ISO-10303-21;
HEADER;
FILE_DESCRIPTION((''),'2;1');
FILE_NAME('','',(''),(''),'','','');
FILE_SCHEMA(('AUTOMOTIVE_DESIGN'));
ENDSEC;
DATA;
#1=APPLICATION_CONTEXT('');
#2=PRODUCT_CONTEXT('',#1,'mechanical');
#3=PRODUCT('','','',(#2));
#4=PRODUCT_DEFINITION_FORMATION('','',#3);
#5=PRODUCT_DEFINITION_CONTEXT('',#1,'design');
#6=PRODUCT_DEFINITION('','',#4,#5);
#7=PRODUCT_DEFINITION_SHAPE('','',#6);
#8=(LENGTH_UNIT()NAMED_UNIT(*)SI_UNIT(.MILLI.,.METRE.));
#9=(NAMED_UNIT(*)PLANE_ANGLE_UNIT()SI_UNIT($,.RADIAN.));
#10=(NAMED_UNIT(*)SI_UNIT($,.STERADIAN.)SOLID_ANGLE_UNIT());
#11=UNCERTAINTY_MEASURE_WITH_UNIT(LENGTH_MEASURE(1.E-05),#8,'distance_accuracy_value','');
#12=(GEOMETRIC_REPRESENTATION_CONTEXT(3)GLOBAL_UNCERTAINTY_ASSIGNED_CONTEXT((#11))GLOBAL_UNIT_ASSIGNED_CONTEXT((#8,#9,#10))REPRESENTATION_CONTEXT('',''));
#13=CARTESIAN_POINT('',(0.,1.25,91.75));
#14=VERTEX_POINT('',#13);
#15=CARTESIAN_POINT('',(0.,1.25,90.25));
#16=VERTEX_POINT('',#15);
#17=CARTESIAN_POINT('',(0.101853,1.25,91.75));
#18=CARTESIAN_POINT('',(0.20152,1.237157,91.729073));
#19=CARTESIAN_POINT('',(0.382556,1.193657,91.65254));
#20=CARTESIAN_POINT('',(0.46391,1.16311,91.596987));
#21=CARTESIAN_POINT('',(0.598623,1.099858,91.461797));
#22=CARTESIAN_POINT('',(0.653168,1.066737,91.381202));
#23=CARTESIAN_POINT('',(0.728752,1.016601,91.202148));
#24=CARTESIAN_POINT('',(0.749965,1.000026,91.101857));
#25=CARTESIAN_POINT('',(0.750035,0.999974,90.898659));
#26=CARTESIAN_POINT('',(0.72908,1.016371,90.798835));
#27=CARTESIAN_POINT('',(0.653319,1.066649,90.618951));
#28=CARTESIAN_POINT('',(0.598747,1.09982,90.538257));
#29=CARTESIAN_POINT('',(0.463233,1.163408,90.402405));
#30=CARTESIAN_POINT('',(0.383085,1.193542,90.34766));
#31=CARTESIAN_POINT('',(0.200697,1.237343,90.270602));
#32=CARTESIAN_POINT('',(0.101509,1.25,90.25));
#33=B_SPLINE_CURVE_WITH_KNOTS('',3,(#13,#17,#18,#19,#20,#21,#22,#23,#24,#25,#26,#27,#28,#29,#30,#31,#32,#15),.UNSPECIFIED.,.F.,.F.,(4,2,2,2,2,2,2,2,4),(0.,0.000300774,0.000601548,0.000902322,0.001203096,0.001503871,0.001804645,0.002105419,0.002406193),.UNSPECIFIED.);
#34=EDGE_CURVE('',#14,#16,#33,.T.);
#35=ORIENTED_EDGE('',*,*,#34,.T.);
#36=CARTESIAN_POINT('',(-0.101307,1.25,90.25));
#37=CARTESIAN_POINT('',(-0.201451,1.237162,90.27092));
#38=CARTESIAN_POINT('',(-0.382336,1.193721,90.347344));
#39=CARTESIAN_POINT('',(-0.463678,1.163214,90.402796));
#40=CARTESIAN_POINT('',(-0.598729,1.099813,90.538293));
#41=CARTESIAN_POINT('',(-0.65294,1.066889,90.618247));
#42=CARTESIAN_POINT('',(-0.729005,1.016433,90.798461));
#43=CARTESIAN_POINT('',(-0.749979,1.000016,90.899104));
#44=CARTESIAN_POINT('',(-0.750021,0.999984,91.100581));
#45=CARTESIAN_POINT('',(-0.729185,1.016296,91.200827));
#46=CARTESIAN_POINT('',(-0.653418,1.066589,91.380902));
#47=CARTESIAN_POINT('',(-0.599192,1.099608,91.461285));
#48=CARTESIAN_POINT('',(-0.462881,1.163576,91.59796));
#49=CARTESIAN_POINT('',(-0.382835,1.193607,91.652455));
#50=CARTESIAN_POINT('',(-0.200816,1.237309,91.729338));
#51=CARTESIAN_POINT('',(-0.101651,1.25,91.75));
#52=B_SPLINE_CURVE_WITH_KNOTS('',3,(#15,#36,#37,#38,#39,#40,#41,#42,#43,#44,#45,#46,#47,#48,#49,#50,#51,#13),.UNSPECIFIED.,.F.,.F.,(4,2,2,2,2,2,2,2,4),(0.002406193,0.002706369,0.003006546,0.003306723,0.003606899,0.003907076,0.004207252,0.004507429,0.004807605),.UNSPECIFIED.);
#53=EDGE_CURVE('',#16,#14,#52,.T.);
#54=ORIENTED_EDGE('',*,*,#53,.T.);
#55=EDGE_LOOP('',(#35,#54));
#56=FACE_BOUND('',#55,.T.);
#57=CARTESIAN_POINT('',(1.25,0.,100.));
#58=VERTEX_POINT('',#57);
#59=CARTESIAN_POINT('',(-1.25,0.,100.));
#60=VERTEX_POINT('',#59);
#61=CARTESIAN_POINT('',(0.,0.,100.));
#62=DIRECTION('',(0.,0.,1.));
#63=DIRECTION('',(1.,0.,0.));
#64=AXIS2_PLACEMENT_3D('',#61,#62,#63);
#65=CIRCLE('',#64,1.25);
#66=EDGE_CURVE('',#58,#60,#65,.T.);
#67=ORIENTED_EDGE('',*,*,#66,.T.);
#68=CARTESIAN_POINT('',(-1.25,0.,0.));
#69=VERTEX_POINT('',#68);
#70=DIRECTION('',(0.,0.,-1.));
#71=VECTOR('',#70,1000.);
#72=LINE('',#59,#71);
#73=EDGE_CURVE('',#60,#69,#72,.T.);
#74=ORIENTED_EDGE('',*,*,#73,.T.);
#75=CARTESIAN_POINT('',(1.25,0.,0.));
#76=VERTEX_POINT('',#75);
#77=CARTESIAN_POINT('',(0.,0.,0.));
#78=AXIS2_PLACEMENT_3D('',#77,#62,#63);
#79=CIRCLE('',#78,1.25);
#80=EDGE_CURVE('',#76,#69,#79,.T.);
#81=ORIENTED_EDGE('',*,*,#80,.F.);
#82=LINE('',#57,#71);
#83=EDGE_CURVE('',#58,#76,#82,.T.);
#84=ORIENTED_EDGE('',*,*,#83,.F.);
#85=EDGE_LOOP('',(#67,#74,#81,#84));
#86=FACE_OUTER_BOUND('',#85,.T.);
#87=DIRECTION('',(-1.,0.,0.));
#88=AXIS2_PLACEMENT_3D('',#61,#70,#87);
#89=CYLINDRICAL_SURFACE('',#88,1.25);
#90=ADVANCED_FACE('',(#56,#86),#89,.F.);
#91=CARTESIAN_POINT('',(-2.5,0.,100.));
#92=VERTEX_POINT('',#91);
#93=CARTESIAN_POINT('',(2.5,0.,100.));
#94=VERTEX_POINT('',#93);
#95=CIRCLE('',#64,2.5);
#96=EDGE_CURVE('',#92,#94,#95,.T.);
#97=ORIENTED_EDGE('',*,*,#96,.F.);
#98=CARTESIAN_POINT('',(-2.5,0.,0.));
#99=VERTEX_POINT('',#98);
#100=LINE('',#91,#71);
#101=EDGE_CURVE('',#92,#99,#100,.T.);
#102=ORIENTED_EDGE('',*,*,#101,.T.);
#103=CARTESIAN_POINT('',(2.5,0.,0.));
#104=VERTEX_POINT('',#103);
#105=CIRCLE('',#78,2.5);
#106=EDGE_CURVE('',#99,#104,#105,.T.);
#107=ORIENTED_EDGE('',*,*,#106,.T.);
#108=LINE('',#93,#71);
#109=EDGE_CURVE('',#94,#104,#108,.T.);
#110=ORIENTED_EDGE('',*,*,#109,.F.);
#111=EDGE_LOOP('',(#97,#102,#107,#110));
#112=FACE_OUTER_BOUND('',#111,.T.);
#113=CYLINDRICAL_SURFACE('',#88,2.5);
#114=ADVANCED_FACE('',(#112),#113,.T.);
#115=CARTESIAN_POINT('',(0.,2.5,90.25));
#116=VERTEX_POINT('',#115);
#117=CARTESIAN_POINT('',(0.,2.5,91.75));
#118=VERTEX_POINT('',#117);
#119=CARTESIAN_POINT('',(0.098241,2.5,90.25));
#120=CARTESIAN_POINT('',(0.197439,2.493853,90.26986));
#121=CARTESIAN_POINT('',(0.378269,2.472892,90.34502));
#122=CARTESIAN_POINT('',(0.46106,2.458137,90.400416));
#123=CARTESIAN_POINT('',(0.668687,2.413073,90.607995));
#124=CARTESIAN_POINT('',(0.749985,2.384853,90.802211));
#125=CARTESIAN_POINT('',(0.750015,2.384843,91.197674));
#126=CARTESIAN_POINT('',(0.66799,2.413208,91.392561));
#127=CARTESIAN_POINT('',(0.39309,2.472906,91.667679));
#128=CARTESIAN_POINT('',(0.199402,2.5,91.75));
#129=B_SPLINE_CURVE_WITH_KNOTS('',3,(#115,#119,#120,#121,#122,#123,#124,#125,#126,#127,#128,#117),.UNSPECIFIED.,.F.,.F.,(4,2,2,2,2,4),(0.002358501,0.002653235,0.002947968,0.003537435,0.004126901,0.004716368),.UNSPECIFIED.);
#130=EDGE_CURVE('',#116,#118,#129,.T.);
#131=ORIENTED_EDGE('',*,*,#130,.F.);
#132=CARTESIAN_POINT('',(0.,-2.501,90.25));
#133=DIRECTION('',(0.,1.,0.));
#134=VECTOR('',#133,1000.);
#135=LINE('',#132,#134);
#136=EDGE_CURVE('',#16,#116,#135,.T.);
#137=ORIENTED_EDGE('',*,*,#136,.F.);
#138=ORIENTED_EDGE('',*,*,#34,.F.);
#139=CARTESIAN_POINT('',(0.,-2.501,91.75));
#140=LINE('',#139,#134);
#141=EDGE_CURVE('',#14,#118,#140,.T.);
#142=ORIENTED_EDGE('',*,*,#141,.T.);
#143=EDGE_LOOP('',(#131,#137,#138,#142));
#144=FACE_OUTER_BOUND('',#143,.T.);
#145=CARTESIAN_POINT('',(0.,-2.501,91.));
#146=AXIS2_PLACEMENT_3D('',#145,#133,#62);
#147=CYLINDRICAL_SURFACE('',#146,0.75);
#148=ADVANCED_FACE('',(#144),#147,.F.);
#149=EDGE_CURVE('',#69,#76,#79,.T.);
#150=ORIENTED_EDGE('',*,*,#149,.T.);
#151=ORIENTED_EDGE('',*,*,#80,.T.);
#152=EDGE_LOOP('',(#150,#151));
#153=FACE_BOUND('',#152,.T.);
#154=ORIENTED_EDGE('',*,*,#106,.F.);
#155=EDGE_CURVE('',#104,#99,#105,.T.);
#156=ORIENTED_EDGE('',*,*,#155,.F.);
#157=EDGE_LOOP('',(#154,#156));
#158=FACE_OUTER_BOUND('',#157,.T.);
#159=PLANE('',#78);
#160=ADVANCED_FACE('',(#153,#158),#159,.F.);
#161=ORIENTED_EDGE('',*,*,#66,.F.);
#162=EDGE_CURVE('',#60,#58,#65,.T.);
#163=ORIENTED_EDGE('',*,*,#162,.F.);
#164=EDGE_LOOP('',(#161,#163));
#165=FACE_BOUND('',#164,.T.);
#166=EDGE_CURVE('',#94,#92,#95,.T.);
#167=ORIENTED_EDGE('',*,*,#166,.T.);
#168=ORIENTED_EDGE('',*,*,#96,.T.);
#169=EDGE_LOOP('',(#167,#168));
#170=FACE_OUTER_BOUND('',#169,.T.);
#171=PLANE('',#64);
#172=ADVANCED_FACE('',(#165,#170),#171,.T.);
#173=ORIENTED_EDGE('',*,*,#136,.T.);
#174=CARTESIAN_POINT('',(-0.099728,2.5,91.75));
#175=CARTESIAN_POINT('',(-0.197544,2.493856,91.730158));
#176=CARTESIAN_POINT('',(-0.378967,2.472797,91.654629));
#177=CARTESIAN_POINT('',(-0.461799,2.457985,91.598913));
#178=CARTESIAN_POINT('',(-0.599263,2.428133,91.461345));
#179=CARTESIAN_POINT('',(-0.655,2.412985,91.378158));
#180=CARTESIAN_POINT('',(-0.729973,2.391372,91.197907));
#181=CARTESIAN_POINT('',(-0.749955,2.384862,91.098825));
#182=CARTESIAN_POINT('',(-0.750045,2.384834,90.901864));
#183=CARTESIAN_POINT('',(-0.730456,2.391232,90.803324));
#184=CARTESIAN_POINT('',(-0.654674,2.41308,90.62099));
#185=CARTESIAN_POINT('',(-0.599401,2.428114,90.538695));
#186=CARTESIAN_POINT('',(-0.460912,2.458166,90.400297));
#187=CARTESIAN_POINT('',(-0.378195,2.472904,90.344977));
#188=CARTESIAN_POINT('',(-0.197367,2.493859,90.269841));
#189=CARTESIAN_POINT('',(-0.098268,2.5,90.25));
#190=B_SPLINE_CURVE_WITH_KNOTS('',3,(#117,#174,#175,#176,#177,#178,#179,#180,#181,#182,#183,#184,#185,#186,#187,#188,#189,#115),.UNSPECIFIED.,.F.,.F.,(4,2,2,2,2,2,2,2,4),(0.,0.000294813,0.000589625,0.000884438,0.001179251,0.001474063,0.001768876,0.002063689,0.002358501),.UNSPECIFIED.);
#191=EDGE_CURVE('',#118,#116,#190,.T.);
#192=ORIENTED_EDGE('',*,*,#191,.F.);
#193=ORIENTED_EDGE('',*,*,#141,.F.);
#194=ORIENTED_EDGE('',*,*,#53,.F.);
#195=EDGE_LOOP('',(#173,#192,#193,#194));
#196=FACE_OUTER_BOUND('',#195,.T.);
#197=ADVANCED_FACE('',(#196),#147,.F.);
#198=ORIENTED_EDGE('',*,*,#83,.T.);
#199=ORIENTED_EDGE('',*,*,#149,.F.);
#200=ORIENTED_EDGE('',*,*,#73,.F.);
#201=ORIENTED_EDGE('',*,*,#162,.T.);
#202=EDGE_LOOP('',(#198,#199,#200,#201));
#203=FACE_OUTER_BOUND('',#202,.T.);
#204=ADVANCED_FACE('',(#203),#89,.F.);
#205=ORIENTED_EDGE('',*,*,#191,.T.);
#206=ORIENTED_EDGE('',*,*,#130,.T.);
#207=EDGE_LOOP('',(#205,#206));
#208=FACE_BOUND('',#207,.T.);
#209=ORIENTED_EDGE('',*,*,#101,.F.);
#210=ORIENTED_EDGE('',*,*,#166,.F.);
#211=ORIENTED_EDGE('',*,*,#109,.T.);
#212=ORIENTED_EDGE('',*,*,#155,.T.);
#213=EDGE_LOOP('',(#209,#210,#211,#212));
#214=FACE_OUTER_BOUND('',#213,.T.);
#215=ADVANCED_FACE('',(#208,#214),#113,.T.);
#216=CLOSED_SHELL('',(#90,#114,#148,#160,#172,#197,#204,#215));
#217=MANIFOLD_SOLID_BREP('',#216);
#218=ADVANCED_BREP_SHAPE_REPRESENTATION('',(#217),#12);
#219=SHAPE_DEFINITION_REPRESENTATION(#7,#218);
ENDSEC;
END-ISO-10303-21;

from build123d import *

# Parameters (mm, degrees)
SKETCH2_R               = 2.5
SKETCH2_R_2             = 1.25
BOSS_EXTRUDE1_DEPTH     = 100
CUT_EXTRUDE1_REACH      = 102.156
CUT_EXTRUDE1_END_RADIUS = 1.25
SKETCH3_R               = 0.75


with BuildPart() as part:
    # Sketch2 → Boss-Extrude1 (new body)
    with BuildSketch(Plane.XY):
        Circle(SKETCH2_R)
        Circle(SKETCH2_R_2, mode=Mode.SUBTRACT)
    extrude(amount=BOSS_EXTRUDE1_DEPTH)

    # Cut-Extrude1: up to this cylinder (the profile starts outside it)
    cut_extrude1_end = Plane(origin=(0, 0, 91), z_dir=(0, 0, -1)) * Cylinder(CUT_EXTRUDE1_END_RADIUS, 207.812, mode=Mode.PRIVATE)
    # Sketch3 → Cut-Extrude1 (cut, up to the surface)
    with BuildSketch(Plane(origin=(0, 2.5, 0), x_dir=(1, 0, 0), z_dir=(0, 1, 0)), mode=Mode.PRIVATE) as cut_extrude1_sk1:
        with Locations(Location((0, -91, 0), (0, 0, 270))):
            Circle(SKETCH3_R)
    cut_extrude1_tool1 = extrude(cut_extrude1_sk1.sketch, amount=-CUT_EXTRUDE1_REACH, mode=Mode.PRIVATE) - cut_extrude1_end
    add(cut_extrude1_tool1.solids().sort_by_distance((0, 2.5, 91))[0], mode=Mode.SUBTRACT)


solid = part.part
